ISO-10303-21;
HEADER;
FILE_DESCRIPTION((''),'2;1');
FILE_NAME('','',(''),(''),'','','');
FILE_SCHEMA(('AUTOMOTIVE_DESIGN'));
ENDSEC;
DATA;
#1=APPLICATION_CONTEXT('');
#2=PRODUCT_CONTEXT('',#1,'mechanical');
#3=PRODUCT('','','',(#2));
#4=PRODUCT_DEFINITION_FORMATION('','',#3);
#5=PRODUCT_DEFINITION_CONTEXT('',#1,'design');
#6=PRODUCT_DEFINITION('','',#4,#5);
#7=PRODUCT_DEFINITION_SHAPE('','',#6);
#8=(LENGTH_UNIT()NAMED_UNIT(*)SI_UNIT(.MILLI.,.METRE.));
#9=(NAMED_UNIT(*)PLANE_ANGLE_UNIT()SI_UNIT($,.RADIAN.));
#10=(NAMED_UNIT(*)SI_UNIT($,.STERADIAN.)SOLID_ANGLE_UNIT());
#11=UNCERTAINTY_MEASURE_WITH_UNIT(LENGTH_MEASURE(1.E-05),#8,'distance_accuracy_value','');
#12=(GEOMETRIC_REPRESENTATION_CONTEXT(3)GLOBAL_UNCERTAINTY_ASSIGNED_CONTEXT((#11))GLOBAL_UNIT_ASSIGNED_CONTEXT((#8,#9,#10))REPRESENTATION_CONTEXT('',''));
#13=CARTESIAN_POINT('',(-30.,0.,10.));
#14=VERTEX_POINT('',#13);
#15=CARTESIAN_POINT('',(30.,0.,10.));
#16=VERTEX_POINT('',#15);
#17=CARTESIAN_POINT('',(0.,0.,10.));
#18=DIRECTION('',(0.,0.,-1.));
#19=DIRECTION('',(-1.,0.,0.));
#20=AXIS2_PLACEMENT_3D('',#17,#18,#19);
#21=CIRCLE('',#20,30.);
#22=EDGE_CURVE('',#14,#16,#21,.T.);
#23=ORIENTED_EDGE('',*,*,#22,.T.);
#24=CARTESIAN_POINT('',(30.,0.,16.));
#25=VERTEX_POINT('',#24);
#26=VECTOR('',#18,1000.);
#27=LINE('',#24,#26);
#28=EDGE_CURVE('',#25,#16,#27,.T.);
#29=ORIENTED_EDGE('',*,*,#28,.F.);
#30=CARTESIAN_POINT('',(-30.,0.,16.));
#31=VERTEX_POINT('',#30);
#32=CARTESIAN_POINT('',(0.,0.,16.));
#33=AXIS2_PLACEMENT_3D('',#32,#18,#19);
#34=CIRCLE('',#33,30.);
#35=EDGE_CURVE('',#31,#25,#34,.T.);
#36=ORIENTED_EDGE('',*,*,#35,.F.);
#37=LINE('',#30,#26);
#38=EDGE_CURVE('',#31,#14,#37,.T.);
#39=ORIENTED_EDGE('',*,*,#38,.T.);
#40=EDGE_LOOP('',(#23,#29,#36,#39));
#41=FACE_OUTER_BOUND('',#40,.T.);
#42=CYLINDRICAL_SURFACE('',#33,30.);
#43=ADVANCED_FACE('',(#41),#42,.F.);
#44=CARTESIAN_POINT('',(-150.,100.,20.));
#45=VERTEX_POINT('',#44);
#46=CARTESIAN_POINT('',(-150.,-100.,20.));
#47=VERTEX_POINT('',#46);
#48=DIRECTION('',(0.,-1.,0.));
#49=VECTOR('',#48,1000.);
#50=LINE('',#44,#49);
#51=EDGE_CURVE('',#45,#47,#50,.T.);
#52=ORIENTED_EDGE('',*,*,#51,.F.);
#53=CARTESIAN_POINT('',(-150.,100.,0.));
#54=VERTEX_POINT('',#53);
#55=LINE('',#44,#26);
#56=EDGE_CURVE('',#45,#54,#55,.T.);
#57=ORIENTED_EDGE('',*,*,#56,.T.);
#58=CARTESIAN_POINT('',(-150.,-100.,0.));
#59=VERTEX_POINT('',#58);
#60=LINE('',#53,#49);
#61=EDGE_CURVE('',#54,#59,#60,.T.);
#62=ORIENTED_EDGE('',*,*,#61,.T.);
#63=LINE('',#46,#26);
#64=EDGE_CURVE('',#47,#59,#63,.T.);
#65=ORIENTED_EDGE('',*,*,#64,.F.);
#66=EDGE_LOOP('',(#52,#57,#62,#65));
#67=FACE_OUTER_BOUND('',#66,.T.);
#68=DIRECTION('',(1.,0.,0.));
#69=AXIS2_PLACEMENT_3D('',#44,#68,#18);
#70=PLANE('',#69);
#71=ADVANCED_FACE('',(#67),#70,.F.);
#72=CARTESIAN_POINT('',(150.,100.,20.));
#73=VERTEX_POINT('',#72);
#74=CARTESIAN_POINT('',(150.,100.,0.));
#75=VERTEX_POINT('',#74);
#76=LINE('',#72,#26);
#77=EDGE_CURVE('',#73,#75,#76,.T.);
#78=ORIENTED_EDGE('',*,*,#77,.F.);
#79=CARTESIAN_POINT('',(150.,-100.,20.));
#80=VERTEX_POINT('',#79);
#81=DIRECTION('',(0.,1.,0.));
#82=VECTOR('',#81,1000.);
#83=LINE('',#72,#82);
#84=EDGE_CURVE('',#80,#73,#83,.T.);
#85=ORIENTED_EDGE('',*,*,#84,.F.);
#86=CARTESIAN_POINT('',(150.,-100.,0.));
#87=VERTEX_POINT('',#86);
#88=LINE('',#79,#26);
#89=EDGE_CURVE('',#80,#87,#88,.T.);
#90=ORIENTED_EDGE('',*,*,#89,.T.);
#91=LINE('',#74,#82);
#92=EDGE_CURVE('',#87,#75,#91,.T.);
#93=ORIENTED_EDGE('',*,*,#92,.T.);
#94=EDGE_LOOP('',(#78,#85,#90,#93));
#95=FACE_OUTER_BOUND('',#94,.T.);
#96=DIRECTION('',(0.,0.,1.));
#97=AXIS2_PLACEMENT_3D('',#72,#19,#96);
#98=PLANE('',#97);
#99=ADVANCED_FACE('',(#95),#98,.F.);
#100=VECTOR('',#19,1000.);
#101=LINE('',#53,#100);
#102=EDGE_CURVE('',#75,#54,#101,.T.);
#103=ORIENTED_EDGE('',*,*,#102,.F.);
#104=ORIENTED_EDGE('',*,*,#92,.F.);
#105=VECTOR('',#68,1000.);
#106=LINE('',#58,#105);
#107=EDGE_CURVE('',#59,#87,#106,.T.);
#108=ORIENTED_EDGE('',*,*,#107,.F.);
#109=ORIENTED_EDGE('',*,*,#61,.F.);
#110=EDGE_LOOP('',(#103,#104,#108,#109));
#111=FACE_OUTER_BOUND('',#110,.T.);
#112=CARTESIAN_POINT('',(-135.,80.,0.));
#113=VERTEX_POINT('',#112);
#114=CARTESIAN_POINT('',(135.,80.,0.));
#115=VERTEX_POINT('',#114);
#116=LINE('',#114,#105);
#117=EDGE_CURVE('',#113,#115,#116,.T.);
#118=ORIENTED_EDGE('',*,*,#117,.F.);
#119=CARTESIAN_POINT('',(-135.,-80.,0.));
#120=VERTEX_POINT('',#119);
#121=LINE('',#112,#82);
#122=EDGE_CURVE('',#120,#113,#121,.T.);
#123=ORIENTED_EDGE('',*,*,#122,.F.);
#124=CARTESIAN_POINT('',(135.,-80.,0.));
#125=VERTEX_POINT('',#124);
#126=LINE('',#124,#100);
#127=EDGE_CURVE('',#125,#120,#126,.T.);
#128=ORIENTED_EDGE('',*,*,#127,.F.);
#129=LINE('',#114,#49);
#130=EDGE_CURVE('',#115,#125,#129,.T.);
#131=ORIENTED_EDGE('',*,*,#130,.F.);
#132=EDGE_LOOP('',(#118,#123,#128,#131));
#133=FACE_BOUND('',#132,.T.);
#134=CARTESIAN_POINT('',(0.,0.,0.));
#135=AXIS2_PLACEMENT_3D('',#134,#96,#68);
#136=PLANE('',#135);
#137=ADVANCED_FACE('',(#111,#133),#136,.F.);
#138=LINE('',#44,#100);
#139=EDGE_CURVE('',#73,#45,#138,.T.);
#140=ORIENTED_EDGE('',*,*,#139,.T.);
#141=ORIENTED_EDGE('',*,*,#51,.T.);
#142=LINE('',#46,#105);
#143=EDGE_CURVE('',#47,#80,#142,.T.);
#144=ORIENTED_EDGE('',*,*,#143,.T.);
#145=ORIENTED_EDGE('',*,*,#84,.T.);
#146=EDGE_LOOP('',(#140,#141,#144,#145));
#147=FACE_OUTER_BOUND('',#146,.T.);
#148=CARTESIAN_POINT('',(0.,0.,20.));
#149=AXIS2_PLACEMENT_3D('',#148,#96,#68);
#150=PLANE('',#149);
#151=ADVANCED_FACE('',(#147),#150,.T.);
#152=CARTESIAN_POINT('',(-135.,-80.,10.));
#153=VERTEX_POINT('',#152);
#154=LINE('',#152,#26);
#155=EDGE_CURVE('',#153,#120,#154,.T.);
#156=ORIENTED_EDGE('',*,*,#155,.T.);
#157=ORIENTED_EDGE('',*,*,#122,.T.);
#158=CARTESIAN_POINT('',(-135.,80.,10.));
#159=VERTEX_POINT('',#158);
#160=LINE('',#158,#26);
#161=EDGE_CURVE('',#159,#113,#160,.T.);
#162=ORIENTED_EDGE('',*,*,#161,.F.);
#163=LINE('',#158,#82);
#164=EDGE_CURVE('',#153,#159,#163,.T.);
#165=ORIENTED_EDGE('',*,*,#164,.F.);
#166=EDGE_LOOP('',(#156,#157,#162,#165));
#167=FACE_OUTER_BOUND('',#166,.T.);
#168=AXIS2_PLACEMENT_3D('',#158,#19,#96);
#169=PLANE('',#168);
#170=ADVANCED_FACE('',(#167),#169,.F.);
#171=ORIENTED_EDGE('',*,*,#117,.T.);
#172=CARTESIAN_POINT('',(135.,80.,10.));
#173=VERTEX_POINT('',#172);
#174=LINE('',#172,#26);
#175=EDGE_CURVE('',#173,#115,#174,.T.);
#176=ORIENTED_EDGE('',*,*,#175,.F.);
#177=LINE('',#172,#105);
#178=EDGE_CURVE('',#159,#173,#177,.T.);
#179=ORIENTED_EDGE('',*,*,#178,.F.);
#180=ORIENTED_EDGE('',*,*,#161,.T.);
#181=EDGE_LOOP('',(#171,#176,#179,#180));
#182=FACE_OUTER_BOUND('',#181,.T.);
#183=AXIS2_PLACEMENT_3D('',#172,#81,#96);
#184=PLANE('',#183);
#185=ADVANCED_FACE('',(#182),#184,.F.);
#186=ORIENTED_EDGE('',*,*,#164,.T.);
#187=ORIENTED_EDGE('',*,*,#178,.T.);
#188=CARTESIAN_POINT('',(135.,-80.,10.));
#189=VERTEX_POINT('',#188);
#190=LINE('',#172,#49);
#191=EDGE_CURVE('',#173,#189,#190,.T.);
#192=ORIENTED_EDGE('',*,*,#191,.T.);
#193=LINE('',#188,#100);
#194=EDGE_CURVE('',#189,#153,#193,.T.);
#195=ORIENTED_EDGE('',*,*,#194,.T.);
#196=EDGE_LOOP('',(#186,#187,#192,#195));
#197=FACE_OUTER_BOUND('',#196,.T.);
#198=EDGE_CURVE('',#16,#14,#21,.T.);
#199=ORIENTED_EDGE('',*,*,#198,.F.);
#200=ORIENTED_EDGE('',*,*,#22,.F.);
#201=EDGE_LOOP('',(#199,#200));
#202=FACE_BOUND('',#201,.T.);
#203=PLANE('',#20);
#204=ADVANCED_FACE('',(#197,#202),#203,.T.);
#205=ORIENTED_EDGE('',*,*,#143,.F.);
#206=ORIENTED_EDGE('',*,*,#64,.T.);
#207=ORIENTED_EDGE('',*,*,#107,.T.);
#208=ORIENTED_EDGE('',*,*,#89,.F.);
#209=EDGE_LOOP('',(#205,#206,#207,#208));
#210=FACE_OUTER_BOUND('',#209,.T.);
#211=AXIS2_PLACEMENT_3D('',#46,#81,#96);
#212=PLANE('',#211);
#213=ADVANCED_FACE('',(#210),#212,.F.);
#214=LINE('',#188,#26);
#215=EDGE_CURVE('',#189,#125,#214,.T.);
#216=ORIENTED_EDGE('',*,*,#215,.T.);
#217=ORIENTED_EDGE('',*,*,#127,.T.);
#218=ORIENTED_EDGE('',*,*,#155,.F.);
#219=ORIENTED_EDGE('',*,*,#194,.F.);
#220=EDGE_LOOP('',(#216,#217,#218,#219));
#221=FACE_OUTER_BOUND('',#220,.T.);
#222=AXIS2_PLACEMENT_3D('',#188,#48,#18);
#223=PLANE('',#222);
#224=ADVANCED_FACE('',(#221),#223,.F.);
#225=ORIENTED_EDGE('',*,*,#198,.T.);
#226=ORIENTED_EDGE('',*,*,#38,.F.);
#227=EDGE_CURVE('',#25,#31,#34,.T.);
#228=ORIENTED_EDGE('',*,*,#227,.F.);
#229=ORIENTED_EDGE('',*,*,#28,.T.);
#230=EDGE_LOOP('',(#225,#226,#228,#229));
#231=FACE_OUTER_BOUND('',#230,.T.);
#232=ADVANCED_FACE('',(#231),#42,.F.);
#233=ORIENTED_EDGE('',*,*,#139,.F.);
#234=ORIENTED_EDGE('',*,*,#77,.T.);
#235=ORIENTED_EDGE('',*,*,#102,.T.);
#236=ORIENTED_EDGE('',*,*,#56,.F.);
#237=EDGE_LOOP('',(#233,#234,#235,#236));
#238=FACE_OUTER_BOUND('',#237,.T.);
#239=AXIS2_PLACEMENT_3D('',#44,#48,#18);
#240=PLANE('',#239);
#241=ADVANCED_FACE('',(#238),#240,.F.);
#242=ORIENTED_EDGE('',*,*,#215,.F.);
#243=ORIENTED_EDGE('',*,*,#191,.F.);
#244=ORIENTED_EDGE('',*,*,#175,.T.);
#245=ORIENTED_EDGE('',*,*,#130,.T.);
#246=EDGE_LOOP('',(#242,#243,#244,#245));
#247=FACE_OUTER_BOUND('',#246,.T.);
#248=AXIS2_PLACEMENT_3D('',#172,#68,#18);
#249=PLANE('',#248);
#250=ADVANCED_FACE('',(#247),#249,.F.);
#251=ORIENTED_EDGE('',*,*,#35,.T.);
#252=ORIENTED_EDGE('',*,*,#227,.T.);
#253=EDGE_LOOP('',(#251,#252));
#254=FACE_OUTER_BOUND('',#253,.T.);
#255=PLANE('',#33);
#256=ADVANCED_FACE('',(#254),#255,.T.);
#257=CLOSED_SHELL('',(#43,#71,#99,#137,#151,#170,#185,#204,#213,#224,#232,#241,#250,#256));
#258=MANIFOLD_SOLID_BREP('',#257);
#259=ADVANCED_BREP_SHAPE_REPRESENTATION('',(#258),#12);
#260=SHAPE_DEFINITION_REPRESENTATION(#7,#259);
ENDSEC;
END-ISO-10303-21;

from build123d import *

# Parameters (mm, degrees)
SKETCH1_W           = 300
SKETCH1_H           = 200
BOSS_EXTRUDE1_DEPTH = 20
SKETCH2_W           = 270
SKETCH2_H           = 160
CUT_EXTRUDE1_DEPTH  = 10
SKETCH3_R           = 30
CUT_EXTRUDE2_DEPTH  = 6


with BuildPart() as part:
    # Sketch1 → Boss-Extrude1 (new body)
    with BuildSketch(Plane.XY):
        Rectangle(SKETCH1_W, SKETCH1_H)
    extrude(amount=BOSS_EXTRUDE1_DEPTH)

    # Sketch2 → Cut-Extrude1 (cut)
    with BuildSketch(Plane(origin=(0, 0, 0), x_dir=(-1, 0, 0), z_dir=(0, 0, -1))):
        Rectangle(SKETCH2_W, SKETCH2_H)
    extrude(amount=-CUT_EXTRUDE1_DEPTH, mode=Mode.SUBTRACT)

    # Sketch3 → Cut-Extrude2 (cut)
    with BuildSketch(Plane(origin=(0, 0, 10), x_dir=(-1, 0, 0), z_dir=(0, 0, -1))):
        Circle(SKETCH3_R)
    extrude(amount=-CUT_EXTRUDE2_DEPTH, mode=Mode.SUBTRACT)


solid = part.part
